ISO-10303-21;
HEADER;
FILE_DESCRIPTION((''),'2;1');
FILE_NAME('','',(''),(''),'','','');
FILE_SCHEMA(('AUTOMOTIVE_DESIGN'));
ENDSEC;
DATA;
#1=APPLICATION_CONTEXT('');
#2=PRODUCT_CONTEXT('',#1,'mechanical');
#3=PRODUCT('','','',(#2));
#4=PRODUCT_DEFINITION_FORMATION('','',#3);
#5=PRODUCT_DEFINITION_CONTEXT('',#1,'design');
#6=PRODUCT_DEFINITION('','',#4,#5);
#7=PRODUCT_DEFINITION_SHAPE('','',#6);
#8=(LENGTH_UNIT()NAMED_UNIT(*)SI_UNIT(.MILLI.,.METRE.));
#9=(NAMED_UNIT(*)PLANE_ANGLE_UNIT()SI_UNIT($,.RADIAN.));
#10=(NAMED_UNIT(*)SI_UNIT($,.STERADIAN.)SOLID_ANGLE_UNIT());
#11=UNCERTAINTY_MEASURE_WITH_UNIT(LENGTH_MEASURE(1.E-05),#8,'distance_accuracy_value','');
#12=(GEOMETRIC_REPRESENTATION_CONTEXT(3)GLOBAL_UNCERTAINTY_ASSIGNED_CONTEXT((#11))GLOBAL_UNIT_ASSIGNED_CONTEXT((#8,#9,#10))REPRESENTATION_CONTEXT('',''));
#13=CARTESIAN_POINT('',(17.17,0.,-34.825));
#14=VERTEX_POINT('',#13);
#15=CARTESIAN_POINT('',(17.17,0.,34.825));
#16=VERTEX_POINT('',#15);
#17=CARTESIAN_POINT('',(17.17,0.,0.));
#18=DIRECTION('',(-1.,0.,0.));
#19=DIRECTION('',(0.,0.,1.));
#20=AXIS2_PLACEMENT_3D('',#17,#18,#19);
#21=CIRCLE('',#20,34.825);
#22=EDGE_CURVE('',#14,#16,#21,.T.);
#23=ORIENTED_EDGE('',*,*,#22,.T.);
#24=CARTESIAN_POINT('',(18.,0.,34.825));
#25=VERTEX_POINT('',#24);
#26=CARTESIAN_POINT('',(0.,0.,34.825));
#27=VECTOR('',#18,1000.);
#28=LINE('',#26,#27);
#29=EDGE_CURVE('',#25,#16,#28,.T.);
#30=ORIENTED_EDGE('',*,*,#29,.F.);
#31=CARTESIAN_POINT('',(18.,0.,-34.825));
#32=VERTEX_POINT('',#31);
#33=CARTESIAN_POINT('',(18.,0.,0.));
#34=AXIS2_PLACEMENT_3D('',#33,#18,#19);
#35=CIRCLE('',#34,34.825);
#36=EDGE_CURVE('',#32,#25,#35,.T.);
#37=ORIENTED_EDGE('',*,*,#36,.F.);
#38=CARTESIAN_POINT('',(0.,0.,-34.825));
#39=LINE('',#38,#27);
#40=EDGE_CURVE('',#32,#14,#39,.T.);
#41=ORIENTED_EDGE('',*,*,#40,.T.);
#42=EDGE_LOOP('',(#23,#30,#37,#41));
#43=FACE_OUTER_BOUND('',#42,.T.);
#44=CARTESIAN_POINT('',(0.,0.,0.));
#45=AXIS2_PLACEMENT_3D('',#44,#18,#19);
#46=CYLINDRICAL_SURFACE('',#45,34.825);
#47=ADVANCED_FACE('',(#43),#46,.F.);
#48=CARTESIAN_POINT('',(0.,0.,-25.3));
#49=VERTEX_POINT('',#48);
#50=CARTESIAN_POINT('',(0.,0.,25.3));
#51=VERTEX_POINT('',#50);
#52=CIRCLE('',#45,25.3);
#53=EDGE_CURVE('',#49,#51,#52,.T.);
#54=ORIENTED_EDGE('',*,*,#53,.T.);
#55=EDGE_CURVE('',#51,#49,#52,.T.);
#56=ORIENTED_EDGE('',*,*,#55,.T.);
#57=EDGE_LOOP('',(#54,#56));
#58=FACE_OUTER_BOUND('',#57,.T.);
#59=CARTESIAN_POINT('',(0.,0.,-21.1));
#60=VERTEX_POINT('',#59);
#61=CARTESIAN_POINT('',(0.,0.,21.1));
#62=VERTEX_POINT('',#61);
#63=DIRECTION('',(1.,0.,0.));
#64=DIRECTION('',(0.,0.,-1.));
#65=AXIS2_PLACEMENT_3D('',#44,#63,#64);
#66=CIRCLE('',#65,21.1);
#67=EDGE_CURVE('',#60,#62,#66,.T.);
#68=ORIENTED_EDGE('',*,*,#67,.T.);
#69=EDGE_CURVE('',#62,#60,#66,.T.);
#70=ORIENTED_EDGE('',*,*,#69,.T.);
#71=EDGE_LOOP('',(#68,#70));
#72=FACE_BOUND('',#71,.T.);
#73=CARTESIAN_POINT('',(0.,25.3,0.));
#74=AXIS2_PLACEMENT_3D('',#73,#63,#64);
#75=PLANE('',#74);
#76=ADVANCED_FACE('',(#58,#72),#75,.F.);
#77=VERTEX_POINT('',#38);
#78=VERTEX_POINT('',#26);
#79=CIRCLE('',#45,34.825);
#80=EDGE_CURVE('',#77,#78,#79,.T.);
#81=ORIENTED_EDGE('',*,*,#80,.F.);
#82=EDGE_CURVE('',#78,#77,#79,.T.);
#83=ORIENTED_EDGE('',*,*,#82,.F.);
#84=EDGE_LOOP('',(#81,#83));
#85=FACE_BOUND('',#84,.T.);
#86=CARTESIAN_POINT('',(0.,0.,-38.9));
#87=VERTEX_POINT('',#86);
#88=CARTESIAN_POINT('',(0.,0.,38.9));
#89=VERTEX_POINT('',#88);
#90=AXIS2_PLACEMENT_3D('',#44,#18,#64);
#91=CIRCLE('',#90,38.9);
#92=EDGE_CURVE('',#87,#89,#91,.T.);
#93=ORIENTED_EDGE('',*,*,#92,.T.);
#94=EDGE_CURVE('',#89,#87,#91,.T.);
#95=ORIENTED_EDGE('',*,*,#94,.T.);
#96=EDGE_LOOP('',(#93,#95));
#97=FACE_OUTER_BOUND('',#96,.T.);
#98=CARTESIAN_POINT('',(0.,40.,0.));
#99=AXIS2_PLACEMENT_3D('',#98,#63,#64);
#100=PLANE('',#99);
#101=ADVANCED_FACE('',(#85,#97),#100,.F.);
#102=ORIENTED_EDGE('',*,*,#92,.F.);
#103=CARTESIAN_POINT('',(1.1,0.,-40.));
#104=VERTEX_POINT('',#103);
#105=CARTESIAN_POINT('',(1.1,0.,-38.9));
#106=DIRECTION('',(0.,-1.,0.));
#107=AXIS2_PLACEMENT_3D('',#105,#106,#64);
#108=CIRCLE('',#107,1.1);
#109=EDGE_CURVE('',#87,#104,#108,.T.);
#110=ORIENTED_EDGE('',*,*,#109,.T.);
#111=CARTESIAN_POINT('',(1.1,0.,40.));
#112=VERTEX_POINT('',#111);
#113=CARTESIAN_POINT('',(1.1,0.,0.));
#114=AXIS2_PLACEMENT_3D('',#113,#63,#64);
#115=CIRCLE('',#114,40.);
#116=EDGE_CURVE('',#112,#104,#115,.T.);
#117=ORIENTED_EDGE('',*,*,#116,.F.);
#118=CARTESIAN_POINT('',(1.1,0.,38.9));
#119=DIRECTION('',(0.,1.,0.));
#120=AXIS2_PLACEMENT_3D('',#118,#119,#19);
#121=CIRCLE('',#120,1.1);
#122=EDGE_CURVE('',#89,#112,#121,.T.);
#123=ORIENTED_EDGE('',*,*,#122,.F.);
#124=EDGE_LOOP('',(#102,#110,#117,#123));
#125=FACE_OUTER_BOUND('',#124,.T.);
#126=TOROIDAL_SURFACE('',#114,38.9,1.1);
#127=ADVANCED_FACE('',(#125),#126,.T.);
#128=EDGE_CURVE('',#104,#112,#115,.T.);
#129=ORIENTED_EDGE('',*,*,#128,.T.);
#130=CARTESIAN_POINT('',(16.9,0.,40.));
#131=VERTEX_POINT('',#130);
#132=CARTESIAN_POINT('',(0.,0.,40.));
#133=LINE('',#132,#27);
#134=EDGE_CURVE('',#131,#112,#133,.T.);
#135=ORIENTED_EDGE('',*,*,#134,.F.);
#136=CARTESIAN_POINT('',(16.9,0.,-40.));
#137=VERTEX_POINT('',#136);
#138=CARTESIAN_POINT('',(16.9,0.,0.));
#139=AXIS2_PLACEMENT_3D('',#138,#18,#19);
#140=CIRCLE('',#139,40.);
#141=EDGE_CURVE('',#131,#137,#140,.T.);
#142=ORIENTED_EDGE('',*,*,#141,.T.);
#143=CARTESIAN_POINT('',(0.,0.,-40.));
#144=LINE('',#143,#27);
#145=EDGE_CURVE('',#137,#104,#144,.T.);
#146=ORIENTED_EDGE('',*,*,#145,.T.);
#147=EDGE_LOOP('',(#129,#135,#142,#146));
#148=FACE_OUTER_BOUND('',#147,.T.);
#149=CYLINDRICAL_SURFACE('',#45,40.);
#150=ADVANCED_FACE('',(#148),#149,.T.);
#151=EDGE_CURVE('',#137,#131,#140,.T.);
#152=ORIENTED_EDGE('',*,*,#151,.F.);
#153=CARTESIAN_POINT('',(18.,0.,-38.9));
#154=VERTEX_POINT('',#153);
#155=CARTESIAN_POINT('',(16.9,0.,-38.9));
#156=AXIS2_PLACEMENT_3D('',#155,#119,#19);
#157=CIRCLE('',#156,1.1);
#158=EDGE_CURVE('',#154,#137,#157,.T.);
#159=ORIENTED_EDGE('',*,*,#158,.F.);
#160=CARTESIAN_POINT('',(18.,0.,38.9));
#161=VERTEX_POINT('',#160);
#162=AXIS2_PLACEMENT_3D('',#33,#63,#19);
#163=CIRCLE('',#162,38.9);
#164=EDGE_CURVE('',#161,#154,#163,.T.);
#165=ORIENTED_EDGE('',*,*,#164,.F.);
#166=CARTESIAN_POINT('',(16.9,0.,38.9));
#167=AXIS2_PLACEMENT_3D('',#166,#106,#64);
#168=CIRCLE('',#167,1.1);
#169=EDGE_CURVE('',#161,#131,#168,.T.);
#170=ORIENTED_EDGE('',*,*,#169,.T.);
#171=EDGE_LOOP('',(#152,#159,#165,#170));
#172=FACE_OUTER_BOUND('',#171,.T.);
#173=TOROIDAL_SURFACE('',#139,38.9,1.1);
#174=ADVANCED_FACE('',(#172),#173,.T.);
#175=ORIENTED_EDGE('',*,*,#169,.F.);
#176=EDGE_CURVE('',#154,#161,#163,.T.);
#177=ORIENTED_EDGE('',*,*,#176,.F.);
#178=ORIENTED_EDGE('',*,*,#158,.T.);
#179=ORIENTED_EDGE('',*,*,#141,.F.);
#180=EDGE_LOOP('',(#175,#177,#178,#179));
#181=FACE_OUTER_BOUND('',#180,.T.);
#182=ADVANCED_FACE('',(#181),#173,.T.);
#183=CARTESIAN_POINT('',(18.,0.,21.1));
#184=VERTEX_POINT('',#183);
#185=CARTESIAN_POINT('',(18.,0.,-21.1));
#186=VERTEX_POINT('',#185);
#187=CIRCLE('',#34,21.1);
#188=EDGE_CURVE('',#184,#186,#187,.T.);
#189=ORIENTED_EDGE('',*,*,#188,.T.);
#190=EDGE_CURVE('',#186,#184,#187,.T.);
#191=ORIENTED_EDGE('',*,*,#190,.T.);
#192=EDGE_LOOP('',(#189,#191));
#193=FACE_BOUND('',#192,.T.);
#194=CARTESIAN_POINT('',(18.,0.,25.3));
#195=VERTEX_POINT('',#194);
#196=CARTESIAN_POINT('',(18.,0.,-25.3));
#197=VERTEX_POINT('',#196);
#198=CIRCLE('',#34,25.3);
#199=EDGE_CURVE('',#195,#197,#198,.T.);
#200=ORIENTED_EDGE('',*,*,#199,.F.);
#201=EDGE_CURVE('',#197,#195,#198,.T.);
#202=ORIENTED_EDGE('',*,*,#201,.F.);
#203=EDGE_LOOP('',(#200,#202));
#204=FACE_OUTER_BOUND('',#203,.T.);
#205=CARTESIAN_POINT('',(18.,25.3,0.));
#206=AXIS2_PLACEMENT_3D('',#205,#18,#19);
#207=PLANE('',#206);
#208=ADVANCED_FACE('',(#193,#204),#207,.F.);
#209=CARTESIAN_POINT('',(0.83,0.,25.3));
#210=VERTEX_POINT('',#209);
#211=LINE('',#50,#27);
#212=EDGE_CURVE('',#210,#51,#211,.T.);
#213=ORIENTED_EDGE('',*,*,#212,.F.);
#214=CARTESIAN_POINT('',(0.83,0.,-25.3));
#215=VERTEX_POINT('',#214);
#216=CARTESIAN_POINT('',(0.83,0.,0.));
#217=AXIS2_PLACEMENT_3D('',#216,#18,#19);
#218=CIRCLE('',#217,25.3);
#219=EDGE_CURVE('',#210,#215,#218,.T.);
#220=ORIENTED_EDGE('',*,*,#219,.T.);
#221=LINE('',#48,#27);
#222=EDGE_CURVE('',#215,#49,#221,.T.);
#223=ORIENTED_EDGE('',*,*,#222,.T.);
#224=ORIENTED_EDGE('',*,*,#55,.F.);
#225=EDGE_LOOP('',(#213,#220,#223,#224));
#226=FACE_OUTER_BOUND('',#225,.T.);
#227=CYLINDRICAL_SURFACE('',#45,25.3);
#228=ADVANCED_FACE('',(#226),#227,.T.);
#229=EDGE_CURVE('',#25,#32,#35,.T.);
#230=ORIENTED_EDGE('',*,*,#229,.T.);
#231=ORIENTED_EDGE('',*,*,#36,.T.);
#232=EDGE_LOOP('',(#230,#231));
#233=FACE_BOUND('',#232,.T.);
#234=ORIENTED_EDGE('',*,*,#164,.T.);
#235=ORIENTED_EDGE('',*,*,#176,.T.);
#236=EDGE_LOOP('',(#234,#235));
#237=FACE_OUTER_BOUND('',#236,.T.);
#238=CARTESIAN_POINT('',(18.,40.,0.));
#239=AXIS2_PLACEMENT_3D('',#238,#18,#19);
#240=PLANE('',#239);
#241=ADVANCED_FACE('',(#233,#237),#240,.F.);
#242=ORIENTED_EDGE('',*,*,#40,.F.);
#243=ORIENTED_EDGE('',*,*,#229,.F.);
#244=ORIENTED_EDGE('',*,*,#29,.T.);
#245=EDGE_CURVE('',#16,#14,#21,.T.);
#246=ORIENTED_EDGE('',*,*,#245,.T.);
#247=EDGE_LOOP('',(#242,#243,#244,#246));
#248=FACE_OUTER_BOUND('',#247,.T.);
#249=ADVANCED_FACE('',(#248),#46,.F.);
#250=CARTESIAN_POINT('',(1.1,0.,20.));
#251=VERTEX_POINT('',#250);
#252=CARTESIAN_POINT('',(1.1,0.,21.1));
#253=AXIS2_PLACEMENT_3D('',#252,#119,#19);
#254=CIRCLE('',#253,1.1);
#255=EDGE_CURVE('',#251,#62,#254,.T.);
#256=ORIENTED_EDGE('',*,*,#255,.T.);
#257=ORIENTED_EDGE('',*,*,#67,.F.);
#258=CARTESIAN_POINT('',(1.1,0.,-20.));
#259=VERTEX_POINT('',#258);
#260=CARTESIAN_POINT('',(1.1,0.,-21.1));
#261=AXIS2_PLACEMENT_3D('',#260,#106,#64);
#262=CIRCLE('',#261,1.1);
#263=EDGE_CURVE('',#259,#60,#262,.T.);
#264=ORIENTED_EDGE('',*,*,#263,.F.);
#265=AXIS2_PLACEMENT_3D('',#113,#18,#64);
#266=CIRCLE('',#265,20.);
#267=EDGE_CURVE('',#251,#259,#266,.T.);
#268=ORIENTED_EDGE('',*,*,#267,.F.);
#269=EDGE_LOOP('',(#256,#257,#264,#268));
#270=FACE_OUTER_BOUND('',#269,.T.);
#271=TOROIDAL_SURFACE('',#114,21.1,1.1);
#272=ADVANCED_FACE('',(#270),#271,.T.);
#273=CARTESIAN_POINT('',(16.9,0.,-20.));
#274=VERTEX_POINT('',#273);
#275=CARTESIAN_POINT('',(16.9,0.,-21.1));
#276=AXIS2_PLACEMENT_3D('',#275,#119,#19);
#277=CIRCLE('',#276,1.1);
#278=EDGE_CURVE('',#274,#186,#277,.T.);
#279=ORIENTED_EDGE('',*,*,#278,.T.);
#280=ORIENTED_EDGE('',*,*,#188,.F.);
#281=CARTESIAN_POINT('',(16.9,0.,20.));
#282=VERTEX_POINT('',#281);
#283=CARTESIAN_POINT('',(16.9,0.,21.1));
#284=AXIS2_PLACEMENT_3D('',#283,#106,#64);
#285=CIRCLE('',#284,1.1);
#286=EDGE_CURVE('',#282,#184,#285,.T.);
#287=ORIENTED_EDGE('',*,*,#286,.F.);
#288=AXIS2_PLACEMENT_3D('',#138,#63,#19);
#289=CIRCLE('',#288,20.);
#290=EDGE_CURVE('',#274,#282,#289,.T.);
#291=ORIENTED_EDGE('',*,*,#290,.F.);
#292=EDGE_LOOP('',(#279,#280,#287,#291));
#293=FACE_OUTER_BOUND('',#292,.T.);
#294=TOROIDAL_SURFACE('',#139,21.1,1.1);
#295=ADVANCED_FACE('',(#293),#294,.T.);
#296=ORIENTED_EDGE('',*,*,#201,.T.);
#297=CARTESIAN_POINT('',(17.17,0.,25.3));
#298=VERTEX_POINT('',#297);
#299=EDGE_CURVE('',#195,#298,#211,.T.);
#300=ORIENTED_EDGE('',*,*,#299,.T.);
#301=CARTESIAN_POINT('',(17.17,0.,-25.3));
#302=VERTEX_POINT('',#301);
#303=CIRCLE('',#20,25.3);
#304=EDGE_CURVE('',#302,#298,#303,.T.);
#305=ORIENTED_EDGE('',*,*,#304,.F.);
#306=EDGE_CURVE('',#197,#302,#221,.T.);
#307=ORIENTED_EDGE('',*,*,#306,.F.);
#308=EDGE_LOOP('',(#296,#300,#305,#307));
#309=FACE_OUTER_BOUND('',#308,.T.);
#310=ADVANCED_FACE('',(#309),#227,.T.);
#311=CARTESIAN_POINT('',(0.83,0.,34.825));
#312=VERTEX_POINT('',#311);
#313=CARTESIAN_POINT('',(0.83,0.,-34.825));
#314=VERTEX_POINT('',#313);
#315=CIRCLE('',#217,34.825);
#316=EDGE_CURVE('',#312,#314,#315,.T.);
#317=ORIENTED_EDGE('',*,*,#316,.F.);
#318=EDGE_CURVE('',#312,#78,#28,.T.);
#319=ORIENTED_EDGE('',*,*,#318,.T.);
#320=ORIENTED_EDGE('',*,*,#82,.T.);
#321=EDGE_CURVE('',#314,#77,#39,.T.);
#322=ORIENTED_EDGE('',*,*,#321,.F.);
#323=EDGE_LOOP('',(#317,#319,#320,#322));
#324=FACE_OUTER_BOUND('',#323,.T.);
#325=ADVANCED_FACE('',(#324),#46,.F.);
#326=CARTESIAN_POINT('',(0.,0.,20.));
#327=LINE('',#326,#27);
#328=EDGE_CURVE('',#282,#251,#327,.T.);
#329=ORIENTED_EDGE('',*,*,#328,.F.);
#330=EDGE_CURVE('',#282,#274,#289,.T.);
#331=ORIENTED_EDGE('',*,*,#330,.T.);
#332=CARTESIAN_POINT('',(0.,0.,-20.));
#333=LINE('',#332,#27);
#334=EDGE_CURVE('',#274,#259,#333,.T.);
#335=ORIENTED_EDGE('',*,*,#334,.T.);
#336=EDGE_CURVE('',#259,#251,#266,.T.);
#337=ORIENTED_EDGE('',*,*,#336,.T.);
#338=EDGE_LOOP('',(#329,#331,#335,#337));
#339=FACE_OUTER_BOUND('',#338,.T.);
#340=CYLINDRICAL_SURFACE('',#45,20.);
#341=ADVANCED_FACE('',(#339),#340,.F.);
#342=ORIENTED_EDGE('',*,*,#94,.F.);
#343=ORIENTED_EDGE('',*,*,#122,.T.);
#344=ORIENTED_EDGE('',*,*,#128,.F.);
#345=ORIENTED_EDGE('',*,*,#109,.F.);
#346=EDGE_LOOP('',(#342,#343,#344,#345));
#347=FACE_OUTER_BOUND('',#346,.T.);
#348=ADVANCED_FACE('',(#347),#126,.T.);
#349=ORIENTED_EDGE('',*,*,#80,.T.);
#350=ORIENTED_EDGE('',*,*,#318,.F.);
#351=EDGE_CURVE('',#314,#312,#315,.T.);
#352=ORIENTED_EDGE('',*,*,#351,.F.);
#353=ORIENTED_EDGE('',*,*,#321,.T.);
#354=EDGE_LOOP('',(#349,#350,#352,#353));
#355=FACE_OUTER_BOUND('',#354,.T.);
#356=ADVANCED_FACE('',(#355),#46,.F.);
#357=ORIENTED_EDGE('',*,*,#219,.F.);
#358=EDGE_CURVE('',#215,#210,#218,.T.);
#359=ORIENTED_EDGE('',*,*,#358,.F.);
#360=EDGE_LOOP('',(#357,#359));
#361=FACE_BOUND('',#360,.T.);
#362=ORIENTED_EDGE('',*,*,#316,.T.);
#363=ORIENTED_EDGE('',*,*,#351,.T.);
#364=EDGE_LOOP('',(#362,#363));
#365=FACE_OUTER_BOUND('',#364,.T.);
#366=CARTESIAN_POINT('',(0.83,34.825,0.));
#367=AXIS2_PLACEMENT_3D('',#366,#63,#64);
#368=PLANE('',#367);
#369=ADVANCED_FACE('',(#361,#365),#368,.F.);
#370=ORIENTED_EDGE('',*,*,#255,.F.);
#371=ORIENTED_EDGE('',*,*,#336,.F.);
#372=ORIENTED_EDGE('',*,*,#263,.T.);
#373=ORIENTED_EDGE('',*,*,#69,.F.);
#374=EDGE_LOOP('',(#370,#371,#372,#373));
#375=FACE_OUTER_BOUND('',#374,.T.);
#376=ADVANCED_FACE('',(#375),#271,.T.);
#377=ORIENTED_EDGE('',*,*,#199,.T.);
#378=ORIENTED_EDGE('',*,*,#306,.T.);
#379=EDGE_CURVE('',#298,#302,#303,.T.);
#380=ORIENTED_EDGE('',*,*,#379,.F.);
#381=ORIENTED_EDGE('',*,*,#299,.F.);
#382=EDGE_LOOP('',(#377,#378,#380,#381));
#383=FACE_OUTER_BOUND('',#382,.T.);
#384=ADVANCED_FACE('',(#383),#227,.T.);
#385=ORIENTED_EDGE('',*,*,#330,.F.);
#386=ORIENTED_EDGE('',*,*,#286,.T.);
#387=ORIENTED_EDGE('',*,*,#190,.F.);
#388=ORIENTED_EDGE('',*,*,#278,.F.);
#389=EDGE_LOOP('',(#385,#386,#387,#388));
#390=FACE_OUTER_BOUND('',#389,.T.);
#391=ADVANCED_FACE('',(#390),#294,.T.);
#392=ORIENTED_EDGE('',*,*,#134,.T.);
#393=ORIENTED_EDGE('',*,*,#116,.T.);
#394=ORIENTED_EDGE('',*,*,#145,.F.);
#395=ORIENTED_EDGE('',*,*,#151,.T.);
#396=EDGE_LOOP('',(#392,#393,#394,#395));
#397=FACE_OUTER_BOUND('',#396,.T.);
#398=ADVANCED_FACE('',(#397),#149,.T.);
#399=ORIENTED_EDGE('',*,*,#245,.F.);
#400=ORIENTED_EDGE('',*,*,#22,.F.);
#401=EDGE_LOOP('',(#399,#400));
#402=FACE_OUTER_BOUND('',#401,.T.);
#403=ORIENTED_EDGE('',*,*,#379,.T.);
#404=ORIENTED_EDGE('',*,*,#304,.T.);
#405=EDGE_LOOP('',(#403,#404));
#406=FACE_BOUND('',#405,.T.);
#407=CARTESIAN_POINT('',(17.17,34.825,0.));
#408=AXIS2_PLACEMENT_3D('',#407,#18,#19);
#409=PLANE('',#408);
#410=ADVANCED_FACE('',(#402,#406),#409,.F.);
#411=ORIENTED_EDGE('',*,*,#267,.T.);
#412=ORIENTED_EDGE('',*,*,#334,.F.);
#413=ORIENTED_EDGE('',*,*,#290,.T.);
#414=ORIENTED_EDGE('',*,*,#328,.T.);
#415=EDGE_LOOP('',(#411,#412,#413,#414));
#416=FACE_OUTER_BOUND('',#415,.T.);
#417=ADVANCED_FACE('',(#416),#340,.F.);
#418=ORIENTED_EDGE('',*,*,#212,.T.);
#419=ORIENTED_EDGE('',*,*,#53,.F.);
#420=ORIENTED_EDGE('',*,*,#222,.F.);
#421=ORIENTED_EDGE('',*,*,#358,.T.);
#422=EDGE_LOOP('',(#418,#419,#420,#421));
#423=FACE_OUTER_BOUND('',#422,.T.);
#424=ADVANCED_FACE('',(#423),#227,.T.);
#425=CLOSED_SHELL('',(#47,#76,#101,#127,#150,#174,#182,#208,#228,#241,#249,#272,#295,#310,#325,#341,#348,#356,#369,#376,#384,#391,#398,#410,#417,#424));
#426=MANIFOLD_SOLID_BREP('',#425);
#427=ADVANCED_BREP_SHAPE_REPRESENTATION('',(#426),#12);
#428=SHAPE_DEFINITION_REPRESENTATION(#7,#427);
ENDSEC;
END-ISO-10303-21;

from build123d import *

# Parameters (mm, degrees)
FILLET1_R = 1.1
FILLET2_R = 1.1


with BuildPart() as part:
    # Sketch1 → Revolve1 (revolve)
    with BuildSketch(Plane.XY, mode=Mode.PRIVATE) as revolve1_sk:
        Polygon((0, 20), (18, 20), (18, 25.3), (17.17, 25.3), (17.17, 34.825), (18, 34.825), (18, 40), (0, 40), (0, 34.825), (0.83, 34.825), (0.83, 25.3), (0, 25.3), align=None)
    revolve(revolve1_sk.sketch.rotate(Axis((0, 0, 0), (1, 0, 0)), 90), axis=Axis((0, 0, 0), (1, 0, 0)))

    # Fillet1
    fillet1_edges = [part.edges().sort_by_distance(p)[0] for p in [
        (0, 0, -40),
        (18, 0, -40),
    ]]
    fillet(fillet1_edges, radius=FILLET1_R)

    # Fillet2
    fillet2_edges = [part.edges().sort_by_distance(p)[0] for p in [
        (18, 0, -20),
        (0, 0, -20),
    ]]
    fillet(fillet2_edges, radius=FILLET2_R)


solid = part.part
